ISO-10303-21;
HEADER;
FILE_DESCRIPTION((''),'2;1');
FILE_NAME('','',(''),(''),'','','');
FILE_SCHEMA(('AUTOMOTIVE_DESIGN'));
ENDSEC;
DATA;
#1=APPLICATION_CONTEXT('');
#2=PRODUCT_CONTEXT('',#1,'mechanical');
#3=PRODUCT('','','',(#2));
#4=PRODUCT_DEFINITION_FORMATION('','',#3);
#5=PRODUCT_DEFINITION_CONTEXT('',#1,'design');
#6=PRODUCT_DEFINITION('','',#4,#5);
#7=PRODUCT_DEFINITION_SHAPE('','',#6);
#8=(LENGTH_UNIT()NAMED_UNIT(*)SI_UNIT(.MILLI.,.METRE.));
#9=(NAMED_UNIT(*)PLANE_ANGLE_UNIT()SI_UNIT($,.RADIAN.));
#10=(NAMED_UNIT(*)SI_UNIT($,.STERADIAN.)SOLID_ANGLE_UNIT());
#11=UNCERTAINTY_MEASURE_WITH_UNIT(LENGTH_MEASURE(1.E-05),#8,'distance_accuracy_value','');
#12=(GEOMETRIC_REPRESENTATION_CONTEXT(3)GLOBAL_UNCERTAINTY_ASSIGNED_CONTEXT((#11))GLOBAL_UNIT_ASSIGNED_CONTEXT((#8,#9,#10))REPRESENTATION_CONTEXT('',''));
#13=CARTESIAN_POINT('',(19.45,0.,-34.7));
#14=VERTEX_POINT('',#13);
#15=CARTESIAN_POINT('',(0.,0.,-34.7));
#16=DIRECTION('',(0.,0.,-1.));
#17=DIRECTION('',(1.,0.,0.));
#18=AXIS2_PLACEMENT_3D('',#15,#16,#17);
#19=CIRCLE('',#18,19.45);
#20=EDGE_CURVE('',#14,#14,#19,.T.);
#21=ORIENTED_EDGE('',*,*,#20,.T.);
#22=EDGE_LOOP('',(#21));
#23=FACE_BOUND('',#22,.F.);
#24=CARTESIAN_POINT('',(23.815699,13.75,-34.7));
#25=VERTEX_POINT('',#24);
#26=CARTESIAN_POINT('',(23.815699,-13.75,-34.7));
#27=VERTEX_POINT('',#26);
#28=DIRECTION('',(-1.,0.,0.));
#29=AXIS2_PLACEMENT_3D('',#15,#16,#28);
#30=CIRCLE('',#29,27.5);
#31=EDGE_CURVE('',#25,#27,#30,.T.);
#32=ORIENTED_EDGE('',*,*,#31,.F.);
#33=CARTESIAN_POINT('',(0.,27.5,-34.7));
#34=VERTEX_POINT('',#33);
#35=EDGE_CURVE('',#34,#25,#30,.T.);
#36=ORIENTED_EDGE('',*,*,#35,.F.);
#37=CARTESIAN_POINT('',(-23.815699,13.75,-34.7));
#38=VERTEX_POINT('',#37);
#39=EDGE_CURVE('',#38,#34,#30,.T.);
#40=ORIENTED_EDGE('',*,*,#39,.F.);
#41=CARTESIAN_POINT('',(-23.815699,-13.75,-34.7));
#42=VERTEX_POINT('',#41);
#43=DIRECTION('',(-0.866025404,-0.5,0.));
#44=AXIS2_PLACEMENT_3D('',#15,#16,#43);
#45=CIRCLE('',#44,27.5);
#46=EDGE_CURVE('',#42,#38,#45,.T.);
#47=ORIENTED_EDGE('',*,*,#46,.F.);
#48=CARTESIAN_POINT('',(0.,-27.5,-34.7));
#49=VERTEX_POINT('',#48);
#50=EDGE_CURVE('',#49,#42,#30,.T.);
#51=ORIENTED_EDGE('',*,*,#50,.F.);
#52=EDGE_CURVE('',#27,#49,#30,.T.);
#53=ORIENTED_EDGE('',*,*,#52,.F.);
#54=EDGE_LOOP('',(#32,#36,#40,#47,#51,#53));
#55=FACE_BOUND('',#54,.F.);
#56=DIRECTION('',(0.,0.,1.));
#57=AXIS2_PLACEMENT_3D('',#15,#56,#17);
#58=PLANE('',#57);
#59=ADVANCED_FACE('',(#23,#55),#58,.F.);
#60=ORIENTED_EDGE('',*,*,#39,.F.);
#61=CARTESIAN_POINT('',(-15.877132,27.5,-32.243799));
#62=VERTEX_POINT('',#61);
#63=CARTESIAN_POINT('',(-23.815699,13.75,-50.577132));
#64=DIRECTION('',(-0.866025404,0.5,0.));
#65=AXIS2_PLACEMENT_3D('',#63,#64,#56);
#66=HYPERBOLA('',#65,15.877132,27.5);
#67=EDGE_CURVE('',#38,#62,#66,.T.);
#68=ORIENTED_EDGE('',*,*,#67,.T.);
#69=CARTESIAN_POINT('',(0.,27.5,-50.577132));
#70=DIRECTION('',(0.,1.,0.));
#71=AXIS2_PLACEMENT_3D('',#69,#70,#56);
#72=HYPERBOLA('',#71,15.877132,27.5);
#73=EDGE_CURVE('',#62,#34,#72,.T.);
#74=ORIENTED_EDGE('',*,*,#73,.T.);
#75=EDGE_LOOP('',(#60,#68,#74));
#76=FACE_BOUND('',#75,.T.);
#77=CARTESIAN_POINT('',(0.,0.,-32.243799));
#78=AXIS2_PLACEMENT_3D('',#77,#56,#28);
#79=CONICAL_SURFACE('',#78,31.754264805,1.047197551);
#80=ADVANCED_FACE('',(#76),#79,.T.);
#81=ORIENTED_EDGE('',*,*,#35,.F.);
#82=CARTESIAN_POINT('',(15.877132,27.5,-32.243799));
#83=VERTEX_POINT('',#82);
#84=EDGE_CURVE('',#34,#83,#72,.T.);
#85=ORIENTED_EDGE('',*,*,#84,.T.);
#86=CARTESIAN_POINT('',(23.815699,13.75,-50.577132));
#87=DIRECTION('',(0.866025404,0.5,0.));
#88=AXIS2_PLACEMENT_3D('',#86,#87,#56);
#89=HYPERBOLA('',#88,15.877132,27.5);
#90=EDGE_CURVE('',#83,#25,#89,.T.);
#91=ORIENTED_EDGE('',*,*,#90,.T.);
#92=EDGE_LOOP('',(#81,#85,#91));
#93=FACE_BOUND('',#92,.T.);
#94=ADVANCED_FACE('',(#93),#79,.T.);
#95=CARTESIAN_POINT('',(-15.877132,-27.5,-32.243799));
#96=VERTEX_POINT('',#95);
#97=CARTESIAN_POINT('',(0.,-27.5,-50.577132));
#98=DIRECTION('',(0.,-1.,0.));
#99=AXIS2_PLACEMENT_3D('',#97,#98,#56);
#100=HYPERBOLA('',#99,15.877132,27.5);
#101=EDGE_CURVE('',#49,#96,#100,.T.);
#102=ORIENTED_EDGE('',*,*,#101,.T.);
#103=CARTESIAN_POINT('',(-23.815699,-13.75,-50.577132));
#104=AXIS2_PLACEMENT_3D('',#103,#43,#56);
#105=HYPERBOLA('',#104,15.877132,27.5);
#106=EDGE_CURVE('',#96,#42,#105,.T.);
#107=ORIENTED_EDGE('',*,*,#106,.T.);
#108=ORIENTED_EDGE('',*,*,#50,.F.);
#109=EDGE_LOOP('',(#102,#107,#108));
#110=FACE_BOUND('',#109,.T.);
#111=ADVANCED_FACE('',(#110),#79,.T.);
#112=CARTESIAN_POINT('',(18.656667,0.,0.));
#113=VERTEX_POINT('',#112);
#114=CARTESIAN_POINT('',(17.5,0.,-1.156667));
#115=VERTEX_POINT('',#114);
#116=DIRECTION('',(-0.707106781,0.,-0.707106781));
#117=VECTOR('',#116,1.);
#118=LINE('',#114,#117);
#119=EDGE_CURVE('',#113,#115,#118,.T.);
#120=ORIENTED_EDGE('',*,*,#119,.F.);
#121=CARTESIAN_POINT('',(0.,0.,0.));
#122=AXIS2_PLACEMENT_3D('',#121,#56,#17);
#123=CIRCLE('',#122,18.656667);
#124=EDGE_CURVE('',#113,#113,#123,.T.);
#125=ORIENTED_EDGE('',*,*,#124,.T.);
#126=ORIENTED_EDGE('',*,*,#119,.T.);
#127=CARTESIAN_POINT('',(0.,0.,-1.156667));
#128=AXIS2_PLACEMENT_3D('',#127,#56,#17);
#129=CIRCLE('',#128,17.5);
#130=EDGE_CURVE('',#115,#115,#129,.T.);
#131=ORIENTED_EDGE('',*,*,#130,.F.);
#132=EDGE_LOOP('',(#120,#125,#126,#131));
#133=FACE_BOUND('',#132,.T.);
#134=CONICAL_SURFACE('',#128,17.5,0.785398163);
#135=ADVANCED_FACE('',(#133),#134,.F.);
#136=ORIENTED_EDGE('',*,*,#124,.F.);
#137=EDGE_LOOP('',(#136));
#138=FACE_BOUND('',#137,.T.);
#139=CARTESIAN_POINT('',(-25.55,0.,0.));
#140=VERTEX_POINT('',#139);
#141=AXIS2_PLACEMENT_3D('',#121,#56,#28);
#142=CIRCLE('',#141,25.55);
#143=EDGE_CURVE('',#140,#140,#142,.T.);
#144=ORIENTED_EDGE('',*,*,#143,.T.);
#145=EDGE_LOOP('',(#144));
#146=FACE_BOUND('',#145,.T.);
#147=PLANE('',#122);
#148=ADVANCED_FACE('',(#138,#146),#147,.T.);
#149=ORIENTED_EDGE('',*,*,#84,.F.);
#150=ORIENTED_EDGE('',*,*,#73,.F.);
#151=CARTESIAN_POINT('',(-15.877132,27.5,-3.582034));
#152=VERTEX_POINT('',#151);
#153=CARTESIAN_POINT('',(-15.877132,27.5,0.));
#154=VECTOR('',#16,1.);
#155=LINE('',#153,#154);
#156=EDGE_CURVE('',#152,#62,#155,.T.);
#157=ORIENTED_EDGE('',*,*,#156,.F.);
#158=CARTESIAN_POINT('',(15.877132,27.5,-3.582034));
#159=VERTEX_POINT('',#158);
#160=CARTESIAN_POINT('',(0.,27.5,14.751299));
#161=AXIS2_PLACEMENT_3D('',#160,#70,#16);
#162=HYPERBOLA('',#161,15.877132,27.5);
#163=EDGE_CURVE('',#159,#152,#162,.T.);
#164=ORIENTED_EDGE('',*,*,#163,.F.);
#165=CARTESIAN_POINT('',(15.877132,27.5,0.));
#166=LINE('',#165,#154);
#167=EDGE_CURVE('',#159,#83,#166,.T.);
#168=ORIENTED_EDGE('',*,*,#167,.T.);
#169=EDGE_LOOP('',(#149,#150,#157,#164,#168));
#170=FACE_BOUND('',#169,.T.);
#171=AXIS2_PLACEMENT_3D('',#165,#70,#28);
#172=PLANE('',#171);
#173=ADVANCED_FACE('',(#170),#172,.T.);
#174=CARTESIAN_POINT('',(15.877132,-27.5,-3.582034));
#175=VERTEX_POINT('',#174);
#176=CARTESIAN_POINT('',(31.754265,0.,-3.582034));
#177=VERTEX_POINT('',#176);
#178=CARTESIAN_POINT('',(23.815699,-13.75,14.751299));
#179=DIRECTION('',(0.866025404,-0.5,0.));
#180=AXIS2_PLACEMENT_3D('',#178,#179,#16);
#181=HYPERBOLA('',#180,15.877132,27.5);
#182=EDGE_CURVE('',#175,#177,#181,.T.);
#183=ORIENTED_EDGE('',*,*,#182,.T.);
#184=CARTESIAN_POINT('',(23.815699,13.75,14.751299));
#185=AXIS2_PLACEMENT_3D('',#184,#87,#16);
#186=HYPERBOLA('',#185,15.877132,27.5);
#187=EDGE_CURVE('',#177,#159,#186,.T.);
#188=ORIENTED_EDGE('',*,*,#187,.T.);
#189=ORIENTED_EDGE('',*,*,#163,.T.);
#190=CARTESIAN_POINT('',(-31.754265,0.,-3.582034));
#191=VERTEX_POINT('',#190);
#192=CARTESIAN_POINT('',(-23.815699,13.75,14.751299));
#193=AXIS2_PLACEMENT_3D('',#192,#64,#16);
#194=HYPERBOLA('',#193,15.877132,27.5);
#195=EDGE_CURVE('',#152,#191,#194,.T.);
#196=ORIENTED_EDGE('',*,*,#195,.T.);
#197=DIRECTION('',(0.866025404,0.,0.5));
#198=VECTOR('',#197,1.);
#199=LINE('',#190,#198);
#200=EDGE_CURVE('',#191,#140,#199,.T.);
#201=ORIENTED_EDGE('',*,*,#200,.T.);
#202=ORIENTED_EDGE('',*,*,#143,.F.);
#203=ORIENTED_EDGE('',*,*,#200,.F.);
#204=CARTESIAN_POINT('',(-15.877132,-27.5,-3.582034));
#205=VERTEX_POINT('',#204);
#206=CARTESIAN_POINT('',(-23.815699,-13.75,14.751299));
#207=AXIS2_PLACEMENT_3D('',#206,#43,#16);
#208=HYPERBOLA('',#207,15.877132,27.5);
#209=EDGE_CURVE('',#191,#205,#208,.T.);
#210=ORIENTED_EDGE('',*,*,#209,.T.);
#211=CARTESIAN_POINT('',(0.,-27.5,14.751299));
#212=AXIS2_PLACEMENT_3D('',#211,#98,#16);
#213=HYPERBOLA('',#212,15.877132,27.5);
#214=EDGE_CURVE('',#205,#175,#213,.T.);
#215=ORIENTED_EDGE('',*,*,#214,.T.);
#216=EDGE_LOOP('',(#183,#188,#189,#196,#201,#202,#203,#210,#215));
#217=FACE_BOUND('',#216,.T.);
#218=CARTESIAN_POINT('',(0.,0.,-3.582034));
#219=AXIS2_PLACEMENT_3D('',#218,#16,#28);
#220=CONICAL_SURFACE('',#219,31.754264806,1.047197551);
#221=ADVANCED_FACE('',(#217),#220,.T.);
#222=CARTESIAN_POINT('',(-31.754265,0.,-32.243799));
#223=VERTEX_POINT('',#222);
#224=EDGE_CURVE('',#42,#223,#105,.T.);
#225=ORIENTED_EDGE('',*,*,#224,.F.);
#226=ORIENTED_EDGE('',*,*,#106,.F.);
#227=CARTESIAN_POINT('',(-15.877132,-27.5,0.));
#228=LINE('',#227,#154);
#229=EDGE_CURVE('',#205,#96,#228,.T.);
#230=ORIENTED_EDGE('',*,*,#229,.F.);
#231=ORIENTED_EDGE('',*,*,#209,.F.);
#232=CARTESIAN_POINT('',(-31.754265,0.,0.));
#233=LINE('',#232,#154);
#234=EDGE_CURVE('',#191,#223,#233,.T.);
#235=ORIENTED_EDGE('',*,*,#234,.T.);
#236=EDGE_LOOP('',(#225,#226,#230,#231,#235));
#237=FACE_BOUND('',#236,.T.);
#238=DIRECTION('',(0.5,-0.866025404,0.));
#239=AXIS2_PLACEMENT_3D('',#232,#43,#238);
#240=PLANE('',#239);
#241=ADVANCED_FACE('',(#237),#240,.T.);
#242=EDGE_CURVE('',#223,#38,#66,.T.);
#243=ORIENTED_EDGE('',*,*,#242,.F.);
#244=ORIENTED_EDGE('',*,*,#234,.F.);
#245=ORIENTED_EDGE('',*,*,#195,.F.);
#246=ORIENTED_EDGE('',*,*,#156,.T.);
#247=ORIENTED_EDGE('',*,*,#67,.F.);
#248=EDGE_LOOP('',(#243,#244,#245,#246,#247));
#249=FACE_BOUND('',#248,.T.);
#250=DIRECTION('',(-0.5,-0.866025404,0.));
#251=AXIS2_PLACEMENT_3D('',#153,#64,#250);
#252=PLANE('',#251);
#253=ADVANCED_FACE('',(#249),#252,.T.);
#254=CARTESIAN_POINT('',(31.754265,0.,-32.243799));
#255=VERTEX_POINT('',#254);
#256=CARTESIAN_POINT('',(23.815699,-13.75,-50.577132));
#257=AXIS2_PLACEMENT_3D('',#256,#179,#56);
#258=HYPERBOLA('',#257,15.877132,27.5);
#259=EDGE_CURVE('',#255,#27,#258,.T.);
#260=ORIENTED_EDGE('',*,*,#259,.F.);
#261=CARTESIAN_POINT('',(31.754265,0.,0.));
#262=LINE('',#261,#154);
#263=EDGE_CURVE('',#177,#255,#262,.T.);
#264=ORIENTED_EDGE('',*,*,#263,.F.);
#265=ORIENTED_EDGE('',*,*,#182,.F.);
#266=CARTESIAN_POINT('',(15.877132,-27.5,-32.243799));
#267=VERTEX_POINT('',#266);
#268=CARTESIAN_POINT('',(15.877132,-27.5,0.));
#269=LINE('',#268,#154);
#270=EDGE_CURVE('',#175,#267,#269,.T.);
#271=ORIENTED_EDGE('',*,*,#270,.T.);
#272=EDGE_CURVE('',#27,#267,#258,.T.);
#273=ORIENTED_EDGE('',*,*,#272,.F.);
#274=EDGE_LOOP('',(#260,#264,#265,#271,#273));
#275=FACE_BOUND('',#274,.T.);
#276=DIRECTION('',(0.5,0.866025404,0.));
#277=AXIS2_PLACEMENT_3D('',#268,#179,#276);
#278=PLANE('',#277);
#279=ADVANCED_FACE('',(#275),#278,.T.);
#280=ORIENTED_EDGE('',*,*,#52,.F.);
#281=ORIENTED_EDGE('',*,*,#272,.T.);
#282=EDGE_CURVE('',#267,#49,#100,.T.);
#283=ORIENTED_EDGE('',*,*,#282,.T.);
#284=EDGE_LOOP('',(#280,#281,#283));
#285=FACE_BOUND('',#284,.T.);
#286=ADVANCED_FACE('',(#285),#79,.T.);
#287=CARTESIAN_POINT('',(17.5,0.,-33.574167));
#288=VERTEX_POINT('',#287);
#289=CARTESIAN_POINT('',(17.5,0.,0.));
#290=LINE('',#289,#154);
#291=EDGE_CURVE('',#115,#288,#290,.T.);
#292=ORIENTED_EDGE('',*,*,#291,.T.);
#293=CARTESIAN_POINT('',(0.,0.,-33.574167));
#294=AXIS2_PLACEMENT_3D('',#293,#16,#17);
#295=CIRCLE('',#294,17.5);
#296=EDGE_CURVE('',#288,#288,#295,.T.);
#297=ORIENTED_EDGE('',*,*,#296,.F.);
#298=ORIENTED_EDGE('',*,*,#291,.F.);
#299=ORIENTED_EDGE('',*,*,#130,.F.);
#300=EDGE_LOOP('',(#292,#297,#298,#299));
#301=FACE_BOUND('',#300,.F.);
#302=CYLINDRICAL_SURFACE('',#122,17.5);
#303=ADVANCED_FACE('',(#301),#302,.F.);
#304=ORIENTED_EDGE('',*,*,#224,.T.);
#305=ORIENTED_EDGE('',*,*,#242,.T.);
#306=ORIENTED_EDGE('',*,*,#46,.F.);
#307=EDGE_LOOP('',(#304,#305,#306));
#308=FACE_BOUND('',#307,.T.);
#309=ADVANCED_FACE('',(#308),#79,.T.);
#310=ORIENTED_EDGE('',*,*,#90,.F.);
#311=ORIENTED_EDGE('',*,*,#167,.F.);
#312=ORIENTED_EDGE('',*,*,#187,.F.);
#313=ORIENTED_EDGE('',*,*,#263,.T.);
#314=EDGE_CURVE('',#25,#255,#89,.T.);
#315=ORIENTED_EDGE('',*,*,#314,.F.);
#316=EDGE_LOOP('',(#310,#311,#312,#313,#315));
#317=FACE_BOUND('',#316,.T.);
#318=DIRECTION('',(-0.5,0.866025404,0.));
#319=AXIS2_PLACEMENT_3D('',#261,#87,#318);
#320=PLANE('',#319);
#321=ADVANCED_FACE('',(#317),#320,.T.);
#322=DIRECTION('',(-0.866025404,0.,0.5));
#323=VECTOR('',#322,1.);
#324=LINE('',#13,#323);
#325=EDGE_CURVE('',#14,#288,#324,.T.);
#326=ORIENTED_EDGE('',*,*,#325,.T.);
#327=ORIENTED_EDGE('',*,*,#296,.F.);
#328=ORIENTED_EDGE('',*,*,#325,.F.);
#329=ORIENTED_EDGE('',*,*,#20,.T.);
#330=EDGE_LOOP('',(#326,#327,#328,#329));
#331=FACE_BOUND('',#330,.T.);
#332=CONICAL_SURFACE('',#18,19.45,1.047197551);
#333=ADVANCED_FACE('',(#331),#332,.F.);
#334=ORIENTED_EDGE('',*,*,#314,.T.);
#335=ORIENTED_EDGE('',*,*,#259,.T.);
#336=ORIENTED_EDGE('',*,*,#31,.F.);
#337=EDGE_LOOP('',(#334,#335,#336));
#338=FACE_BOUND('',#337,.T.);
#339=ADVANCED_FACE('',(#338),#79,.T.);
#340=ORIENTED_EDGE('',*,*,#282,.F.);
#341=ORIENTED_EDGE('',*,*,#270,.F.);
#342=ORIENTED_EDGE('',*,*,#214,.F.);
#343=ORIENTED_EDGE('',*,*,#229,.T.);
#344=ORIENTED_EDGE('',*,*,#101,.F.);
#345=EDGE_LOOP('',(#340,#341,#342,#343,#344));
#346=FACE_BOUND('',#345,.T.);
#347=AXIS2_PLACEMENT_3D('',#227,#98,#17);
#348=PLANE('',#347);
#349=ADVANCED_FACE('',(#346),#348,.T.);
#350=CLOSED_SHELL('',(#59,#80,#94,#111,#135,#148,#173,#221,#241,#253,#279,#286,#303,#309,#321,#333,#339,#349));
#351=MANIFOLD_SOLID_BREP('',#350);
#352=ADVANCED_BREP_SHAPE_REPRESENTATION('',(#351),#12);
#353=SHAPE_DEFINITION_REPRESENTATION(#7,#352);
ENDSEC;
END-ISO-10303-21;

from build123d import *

# Parameters (mm, degrees)
SKETCH1_R        = 17.5
BASENUT_DEPTH    = 34.7
ENDCHAMFER2_SIZE = 1.156666667


with BuildPart() as part:
    # Sketch1 → BaseNut (new body)
    with BuildSketch(Plane.XY):
        Polygon((15.877132403, -27.5), (31.754264805, 0), (15.877132403, 27.5), (-15.877132403, 27.5), (-31.754264805, 0), (-15.877132403, -27.5), align=None)
        Circle(SKETCH1_R, mode=Mode.SUBTRACT)
    extrude(amount=-BASENUT_DEPTH)

    # Sketch2 → Chamfer1 (revolve, cut)
    with BuildSketch(Plane(origin=(15.04811501, 0, -16.706149795), x_dir=(0, 0, -1), z_dir=(0, 1, 0))):
        Polygon((15.537649274, 46.802379815), (17.993850205, 42.54811501), (17.993850205, 46.802379815), align=None)
    revolve(axis=Axis((0, 0, 7.016501752), (0, 0, -1)), mode=Mode.SUBTRACT)

    # Sketch6 → EndChamfer1 (revolve, cut)
    with BuildSketch(Plane(origin=(-9.197458863, 0, -10.252541137), x_dir=(0, 0, 1), z_dir=(0, 1, 0))):
        Polygon((-24.447458863, 26.697458863), (-24.447458863, 28.647458863), (-23.321625838, 26.697458863), align=None)
    revolve(axis=Axis((0, 0, 13.104863586), (0, 0, -1)), mode=Mode.SUBTRACT)

    # Sketch5 → Chamfer2 (revolve, cut)
    with BuildSketch(Plane(origin=(-14.793032735, 0, -16.96123207), x_dir=(0, 0, 1), z_dir=(0, 1, 0)), mode=Mode.PRIVATE) as chamfer2_sk:
        Polygon((16.96123207, 40.343032735), (16.96123207, 46.547297541), (13.379198115, 46.547297541), align=None)
    revolve(chamfer2_sk.sketch.rotate(Axis((0, 0, -39.536013381), (0, 0, 1)), 180), axis=Axis((0, 0, -39.536013381), (0, 0, 1)), mode=Mode.SUBTRACT)

    # EndChamfer2
    endchamfer2_edges = [part.edges().sort_by_distance(p)[0] for p in [
        (-17.5, 0, 0),
    ]]
    chamfer(endchamfer2_edges, length=ENDCHAMFER2_SIZE)


solid = part.part
